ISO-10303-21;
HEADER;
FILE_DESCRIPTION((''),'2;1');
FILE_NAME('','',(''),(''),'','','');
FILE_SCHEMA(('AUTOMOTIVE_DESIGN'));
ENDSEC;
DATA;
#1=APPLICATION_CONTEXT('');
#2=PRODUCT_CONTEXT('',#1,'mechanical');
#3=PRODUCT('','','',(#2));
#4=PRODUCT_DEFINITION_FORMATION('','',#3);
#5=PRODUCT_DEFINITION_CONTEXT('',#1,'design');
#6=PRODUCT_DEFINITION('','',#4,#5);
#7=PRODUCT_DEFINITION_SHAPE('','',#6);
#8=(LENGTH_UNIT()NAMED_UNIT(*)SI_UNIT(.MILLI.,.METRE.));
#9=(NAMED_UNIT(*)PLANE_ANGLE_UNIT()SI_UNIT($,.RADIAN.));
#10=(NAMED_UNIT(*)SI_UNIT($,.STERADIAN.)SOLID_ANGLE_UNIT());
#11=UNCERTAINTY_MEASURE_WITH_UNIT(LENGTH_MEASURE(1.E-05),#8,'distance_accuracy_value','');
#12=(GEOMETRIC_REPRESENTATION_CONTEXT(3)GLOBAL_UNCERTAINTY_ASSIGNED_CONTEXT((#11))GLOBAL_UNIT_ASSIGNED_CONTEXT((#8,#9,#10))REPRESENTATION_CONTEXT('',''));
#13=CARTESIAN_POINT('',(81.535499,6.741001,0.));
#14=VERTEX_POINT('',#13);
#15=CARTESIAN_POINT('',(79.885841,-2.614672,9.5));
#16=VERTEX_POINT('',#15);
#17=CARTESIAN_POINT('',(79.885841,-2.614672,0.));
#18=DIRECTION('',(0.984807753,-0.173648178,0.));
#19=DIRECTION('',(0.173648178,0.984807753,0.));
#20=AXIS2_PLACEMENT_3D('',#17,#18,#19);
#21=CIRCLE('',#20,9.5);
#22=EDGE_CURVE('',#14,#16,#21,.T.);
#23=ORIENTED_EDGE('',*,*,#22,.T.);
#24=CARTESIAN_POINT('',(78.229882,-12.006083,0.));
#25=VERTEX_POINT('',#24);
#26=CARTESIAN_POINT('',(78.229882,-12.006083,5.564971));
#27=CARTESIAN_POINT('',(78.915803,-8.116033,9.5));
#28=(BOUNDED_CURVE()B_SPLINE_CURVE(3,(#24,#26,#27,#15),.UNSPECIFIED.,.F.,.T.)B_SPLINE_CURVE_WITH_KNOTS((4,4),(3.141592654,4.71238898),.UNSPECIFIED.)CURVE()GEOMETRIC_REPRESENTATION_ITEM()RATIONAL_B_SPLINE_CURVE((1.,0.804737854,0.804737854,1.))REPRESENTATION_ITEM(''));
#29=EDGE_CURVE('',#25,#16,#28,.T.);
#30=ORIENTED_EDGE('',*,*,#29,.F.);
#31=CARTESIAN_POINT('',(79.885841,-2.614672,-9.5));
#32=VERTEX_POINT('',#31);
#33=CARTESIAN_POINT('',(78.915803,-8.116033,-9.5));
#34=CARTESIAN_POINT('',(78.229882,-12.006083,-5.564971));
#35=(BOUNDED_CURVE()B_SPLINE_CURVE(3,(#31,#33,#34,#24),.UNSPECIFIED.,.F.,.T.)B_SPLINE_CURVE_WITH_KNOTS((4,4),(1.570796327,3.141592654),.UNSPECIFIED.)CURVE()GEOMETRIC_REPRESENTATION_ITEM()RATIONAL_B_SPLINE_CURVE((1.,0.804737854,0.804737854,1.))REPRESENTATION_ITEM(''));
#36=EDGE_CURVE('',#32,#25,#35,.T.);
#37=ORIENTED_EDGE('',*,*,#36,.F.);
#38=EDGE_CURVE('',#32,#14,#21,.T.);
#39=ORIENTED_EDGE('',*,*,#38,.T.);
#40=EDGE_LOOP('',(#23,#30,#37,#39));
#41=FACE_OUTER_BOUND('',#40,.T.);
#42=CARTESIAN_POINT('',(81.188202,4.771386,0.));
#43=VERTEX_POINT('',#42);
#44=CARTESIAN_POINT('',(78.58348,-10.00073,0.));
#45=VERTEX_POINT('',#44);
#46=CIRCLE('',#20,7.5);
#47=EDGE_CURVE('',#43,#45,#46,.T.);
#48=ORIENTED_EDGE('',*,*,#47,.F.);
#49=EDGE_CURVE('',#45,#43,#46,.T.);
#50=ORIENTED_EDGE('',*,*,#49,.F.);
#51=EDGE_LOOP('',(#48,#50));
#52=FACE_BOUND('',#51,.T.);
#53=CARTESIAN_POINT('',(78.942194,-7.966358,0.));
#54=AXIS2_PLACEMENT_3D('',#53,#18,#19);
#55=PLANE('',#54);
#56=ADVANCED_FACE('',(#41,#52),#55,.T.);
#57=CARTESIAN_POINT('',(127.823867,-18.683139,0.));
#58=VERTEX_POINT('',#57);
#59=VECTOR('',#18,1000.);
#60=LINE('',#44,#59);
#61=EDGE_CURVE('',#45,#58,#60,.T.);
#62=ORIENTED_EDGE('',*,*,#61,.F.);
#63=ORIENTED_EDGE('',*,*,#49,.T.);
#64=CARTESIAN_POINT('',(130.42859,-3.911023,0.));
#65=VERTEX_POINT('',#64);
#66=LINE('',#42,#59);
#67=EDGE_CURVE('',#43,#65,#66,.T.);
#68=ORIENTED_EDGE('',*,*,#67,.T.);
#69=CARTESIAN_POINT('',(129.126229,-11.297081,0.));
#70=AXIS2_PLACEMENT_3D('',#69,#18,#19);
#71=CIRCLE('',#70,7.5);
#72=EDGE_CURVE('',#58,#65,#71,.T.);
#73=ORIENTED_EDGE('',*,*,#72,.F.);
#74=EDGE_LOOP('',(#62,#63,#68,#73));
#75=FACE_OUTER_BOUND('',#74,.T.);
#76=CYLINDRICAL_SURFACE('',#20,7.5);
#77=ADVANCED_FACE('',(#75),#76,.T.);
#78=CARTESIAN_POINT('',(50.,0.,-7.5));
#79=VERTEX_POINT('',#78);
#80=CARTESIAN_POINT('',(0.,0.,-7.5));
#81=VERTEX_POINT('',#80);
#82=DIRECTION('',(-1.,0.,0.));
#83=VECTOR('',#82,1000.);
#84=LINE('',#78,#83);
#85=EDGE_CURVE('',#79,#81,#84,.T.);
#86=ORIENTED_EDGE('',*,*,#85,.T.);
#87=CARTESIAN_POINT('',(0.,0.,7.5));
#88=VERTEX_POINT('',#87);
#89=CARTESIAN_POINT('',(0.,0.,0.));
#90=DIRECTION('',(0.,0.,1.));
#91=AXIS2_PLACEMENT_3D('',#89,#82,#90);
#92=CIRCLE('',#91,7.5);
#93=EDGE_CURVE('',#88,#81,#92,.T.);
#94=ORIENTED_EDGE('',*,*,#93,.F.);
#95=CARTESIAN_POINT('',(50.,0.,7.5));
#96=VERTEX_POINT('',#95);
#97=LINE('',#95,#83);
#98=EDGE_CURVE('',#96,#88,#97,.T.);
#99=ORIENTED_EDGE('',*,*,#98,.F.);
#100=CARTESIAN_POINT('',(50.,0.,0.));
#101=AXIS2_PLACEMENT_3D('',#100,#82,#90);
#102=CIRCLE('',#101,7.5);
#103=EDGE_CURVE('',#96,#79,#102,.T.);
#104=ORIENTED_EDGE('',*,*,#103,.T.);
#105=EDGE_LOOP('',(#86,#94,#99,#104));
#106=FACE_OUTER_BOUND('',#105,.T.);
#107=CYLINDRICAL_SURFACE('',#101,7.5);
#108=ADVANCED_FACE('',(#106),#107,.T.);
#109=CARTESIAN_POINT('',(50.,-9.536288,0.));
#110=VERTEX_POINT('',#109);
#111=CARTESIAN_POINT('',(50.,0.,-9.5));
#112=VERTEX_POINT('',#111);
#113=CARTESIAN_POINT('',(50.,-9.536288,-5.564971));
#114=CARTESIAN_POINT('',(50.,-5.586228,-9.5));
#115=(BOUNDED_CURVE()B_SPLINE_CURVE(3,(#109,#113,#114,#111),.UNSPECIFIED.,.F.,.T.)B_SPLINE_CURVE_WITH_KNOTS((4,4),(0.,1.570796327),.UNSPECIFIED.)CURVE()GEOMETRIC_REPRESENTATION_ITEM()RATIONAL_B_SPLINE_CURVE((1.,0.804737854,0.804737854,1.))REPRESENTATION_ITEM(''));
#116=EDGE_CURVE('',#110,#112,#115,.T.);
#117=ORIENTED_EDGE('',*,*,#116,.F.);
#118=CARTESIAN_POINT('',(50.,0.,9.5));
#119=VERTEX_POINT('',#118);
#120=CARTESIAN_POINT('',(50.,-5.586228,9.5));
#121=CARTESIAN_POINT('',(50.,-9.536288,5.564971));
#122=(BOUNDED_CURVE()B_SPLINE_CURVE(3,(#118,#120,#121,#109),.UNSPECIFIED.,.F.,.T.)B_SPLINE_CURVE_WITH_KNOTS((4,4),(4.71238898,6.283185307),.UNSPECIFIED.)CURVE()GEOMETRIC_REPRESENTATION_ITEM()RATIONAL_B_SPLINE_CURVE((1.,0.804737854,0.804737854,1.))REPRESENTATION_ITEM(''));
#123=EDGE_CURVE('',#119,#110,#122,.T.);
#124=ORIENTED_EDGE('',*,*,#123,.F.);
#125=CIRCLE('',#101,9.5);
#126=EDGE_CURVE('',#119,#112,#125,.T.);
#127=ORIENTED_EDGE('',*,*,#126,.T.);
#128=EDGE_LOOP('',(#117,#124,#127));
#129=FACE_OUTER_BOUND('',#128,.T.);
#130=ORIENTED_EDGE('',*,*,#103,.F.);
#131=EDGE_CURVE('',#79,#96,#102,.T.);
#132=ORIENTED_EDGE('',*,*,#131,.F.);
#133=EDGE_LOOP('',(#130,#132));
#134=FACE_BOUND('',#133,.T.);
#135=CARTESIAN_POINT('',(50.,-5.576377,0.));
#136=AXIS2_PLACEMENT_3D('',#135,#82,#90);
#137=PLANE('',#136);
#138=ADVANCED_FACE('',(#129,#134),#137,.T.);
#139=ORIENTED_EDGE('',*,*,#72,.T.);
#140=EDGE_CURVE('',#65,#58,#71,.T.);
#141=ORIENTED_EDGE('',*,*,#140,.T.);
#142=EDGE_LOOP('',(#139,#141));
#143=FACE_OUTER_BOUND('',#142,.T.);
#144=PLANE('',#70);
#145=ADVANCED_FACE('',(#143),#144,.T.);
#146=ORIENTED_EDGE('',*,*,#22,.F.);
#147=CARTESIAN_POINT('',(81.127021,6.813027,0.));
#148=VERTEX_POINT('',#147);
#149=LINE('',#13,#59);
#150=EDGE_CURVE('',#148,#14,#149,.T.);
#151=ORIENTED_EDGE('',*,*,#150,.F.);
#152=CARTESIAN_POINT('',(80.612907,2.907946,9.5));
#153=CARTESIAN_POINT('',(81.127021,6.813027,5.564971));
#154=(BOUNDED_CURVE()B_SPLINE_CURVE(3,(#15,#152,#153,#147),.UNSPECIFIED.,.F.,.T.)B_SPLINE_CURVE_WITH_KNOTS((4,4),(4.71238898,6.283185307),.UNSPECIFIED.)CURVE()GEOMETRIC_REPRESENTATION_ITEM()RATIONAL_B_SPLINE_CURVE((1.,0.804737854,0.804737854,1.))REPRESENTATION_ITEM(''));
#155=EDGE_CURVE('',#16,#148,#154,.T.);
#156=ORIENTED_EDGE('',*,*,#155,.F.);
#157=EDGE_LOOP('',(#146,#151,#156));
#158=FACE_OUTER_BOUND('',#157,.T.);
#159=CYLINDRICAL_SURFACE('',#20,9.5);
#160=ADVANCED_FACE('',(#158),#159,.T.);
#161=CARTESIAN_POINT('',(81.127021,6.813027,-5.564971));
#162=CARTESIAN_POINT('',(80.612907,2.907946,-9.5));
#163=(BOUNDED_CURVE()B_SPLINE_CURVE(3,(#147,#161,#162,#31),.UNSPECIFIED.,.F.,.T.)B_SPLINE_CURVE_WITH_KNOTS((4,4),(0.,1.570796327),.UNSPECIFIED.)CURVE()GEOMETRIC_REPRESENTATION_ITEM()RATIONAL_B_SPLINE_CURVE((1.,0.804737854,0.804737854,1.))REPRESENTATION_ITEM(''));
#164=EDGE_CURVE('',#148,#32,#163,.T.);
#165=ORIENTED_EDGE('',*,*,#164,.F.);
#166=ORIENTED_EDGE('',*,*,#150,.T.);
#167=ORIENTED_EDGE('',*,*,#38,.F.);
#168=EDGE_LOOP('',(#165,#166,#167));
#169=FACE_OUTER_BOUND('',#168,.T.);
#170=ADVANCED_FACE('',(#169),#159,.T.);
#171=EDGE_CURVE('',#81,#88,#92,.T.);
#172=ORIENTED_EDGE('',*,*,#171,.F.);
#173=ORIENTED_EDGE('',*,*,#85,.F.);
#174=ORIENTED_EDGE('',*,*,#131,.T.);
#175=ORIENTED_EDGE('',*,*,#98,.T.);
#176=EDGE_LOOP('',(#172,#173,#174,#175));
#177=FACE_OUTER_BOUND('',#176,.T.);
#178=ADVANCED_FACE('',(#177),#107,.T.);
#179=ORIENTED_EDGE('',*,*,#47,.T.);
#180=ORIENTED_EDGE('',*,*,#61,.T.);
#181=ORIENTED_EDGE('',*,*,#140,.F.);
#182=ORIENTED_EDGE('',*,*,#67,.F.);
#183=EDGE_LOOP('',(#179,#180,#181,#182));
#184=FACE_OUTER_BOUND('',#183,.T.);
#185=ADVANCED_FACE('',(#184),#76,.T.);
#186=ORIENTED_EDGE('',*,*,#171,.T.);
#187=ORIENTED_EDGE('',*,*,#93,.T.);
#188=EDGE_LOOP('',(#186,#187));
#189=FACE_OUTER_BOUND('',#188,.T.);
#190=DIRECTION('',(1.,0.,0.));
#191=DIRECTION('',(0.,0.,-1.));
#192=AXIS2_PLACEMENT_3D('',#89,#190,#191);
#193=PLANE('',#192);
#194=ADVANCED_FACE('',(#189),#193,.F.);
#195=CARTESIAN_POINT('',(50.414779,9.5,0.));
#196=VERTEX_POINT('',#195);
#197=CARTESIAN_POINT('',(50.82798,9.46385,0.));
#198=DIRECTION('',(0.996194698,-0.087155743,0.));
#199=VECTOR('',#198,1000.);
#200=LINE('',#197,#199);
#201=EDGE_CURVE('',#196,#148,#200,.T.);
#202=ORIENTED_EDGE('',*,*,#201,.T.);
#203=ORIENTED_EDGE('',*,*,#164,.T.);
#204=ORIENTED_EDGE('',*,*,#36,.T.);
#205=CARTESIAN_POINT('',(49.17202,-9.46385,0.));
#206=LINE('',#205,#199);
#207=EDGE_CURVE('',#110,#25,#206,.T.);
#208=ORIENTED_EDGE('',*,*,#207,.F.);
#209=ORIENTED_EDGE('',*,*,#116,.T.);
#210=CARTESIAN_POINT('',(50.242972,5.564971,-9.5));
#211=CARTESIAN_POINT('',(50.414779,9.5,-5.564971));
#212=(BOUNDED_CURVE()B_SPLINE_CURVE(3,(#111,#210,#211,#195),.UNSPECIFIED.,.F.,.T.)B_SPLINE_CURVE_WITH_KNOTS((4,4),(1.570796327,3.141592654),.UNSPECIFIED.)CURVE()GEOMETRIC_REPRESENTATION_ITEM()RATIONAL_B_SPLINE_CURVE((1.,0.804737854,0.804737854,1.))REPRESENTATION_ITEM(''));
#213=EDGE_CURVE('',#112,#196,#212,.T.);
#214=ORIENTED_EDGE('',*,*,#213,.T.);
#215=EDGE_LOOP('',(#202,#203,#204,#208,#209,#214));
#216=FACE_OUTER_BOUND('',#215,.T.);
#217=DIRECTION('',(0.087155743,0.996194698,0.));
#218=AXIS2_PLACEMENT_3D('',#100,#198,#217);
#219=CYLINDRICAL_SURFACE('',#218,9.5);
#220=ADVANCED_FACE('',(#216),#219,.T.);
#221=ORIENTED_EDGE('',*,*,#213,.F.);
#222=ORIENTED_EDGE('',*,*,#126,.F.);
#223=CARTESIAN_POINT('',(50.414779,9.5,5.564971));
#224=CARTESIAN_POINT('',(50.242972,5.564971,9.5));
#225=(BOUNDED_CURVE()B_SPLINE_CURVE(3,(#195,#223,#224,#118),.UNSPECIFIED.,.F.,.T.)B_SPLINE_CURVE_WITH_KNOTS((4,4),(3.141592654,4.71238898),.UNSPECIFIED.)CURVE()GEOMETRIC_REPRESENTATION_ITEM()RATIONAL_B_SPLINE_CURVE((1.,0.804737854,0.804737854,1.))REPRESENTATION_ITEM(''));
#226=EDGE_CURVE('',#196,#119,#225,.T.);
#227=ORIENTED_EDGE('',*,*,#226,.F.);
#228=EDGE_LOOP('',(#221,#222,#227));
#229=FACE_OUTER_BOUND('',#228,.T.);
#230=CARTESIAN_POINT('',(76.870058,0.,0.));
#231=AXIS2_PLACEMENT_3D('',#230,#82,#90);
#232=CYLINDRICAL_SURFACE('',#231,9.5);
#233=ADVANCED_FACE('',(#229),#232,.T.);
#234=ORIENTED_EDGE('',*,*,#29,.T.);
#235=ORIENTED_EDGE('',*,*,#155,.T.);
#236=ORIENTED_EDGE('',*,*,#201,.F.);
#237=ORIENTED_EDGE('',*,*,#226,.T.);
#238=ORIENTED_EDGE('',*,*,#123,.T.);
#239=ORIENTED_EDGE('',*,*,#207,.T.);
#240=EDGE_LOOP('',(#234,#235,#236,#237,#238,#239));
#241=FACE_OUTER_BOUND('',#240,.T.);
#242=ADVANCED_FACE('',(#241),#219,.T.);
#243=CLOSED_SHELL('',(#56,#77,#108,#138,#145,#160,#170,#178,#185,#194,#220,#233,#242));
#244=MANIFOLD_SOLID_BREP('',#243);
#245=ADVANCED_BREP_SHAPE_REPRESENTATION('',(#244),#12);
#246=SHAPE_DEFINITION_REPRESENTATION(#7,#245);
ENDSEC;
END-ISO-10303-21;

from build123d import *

# Parameters (mm, degrees)
SKETCH_2_R          = 9.5
SKETCH_3_OUTSIDE_W  = 48.11
SKETCH_3_OUTSIDE_H  = 59.263
SKETCH_3_OUTSIDE_R  = 7.5
CUT_EXTRUDE_1_DEPTH = 50
SKETCH_4_OUTSIDE_W  = 48.11
SKETCH_4_OUTSIDE_H  = 81.514
SKETCH_4_OUTSIDE_R  = 7.5
CUT_EXTRUDE_2_DEPTH = 50


with BuildPart() as part:
    # 扫描1: sweep along a path in 草图1
    with BuildLine(Plane.XY) as sweep_1_path:
        Line((0, 0), (50, 0))
        Line((50, 0), (79.885840943, -2.614672282))
        Line((79.885840943, -2.614672282), (129.126228593, -11.297081166))
    # 草图2 → 扫描1 (sweep)
    with BuildSketch(Plane(origin=(0, 0, 0), x_dir=(0, 0, -1), z_dir=(1, 0, 0))):
        Circle(SKETCH_2_R)
    sweep(path=sweep_1_path.line, transition=Transition.RIGHT)

    # 草图3 outside → 切除-拉伸1 (cut)
    with BuildSketch(Plane.ZY):
        with Locations((0, -5.5765)):
            Rectangle(SKETCH_3_OUTSIDE_W, SKETCH_3_OUTSIDE_H)
        Circle(SKETCH_3_OUTSIDE_R, mode=Mode.SUBTRACT)
    extrude(amount=-CUT_EXTRUDE_1_DEPTH, mode=Mode.SUBTRACT)

    # 草图4 outside → 切除-拉伸2 (cut)
    with BuildSketch(Plane(origin=(127.164511036, -22.422534284, 0), x_dir=(0, 0, -1), z_dir=(0.984807753012208, -0.173648177666931, 0))):
        with Locations((0, 5.863)):
            Rectangle(SKETCH_4_OUTSIDE_W, SKETCH_4_OUTSIDE_H)
        with Locations(Location((0, 11.297081166, 0), (0, 0, 90))):
            Circle(SKETCH_4_OUTSIDE_R, mode=Mode.SUBTRACT)
    extrude(amount=-CUT_EXTRUDE_2_DEPTH, mode=Mode.SUBTRACT)


solid = part.part
